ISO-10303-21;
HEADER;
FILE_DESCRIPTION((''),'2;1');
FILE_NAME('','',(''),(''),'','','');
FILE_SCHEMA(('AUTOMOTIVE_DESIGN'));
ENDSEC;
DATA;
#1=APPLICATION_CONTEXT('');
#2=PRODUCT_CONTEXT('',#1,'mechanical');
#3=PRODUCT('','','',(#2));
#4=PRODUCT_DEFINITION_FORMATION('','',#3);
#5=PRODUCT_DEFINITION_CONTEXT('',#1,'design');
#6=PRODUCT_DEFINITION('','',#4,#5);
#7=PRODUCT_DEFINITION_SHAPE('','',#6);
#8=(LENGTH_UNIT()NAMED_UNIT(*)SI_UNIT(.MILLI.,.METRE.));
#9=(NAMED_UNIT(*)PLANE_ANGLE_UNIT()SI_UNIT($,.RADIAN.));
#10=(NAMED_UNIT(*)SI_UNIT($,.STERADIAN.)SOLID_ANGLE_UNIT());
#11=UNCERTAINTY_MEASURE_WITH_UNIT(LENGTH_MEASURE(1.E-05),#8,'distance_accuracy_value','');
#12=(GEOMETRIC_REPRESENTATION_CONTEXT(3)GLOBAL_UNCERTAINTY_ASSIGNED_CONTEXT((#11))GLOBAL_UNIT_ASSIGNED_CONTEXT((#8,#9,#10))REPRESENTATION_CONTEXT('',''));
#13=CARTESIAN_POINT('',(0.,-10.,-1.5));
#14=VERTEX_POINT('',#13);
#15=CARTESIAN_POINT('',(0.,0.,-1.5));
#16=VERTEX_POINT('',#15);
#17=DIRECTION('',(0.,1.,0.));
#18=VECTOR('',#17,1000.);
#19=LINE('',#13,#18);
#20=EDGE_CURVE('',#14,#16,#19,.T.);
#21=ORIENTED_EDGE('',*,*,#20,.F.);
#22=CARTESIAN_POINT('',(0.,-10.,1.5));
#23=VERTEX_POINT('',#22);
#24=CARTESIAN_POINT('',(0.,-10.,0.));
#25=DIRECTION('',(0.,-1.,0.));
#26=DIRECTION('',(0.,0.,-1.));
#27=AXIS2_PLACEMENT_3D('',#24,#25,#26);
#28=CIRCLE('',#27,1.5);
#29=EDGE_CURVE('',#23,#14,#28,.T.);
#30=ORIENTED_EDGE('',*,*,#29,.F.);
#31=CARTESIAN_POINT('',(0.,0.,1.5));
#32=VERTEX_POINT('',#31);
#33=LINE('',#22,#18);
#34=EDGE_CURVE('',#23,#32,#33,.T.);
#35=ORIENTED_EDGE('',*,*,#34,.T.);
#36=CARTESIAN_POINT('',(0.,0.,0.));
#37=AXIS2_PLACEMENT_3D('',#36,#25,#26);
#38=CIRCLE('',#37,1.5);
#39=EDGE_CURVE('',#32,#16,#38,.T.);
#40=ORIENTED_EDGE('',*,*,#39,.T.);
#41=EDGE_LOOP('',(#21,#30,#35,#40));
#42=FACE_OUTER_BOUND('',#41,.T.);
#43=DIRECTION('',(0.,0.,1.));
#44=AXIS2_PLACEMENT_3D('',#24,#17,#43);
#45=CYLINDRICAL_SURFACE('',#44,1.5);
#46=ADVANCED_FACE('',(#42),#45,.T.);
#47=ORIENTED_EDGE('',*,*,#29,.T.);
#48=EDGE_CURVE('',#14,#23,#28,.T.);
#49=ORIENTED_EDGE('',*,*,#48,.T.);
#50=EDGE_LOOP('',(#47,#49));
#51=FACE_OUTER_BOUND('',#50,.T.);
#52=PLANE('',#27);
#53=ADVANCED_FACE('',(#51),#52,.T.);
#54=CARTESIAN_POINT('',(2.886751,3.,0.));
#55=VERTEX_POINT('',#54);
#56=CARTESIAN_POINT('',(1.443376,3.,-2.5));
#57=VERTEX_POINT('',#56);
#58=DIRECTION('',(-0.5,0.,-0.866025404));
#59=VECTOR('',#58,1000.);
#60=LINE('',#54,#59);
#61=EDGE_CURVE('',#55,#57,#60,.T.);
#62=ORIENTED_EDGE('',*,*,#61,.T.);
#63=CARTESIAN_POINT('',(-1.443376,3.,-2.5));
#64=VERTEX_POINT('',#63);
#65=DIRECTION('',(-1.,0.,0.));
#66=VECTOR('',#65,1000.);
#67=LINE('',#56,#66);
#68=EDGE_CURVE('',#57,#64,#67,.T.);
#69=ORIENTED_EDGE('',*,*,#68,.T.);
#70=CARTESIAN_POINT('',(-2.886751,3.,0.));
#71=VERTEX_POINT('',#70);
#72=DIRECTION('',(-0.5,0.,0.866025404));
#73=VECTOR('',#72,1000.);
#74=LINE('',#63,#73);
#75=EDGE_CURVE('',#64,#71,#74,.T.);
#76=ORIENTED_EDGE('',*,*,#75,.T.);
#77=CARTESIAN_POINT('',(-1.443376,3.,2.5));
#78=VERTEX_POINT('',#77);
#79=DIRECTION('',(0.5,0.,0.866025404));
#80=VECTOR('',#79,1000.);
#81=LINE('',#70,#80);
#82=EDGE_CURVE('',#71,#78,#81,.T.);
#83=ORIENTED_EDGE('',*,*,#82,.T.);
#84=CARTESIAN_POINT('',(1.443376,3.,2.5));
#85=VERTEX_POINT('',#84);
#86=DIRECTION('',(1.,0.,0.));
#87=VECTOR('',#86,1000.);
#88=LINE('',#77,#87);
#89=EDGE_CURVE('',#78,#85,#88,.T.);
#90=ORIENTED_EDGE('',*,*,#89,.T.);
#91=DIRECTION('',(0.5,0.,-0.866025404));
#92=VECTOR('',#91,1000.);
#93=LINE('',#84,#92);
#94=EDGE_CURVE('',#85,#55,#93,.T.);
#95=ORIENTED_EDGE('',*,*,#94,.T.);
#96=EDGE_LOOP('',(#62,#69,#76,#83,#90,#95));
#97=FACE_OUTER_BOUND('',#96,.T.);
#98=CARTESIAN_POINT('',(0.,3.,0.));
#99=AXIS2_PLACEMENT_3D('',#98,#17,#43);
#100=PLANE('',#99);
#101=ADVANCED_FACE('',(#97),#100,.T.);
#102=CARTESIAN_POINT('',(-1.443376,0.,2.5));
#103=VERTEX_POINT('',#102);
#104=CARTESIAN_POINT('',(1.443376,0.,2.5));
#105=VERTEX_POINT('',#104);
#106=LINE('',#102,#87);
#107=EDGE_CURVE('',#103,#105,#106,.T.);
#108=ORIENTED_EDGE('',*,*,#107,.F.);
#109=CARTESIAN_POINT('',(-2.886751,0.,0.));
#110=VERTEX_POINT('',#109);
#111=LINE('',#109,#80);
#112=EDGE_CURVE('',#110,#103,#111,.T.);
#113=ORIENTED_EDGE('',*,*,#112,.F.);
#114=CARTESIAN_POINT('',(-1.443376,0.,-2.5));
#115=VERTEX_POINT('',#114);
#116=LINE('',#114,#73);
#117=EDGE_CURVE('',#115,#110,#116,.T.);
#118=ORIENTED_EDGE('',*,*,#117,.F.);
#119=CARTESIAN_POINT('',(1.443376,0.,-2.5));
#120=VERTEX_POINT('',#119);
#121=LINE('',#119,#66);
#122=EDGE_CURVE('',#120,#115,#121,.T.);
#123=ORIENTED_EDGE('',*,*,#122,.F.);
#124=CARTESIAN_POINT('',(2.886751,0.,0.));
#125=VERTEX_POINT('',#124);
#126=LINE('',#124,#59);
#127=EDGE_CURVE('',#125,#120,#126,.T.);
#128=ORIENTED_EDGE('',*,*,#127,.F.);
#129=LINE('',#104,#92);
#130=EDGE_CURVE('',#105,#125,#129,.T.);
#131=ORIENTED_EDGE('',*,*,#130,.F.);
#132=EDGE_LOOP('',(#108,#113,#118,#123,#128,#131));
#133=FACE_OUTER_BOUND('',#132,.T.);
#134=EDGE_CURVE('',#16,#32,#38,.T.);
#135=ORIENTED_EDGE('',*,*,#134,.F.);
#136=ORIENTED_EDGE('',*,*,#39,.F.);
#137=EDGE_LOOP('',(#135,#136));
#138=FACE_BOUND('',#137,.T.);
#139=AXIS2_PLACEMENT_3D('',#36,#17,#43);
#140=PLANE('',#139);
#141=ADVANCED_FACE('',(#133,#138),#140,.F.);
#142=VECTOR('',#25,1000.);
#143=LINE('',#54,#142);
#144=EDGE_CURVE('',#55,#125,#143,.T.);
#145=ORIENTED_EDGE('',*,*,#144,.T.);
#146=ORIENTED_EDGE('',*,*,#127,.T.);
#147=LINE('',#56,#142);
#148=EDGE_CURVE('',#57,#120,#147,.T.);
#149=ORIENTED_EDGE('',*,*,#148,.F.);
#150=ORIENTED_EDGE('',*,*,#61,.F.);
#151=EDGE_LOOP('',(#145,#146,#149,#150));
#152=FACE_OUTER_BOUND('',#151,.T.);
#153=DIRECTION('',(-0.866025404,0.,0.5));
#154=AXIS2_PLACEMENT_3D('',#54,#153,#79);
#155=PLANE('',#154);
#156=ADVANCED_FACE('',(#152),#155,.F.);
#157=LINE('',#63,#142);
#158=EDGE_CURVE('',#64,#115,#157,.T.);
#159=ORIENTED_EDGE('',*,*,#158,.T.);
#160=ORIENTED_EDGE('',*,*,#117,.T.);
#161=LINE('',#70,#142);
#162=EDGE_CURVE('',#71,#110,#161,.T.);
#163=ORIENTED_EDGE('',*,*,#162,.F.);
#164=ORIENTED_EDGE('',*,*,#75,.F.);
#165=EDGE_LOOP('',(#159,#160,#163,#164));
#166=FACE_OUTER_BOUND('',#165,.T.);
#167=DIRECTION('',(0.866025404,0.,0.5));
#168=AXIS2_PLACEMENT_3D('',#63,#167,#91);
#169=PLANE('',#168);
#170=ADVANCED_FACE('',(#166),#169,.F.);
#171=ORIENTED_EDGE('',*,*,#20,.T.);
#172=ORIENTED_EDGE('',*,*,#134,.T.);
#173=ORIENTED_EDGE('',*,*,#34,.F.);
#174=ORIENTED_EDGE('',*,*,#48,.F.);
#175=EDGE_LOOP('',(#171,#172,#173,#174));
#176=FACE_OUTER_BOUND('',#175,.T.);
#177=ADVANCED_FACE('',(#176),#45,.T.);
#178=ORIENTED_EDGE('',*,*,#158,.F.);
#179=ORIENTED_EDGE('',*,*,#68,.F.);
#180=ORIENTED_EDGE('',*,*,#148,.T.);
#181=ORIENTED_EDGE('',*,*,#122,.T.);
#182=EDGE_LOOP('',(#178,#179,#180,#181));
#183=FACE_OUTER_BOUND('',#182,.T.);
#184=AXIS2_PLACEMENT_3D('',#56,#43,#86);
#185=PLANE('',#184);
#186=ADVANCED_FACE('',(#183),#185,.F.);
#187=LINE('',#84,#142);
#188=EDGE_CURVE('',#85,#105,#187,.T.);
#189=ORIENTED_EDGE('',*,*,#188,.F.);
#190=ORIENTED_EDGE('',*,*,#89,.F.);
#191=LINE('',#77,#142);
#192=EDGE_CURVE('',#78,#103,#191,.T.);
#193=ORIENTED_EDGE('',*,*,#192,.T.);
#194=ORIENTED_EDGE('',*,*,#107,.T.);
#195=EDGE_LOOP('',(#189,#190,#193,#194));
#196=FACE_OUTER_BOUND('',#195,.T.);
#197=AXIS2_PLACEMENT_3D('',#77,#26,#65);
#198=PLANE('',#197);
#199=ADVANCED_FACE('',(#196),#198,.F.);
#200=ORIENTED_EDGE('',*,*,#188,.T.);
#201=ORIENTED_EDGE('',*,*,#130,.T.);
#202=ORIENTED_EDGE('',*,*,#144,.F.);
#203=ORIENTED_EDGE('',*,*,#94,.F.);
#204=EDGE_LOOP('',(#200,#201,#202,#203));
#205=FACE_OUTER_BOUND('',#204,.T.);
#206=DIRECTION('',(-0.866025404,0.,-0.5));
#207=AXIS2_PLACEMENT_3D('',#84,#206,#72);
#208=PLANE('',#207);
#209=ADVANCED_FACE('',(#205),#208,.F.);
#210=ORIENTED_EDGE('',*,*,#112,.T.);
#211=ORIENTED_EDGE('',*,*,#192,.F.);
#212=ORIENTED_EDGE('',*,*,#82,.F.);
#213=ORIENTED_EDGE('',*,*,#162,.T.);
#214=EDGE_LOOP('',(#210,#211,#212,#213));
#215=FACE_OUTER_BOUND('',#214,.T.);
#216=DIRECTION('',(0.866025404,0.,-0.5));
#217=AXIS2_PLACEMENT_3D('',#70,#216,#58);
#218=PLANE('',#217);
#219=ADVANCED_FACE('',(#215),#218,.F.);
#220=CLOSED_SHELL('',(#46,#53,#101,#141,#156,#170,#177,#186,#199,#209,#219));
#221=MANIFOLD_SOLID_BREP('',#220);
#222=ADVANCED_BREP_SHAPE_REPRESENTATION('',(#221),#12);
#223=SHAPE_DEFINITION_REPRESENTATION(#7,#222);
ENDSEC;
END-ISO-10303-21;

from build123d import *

# Parameters (mm, degrees)
HEX_HEAD_5AF_X_3_DEPTH = 3
SHANK_PROFILE_3_R      = 1.5
SHANK_3_X_10_DEPTH     = 10


with BuildPart() as part:
    # Hex Head Profile → Hex Head 5AF x 3 (new body)
    with BuildSketch(Plane(origin=(0, 0, 0), x_dir=(1, 0, 0), z_dir=(0, 1, 0))):
        Polygon((2.886751346, 0), (1.443375673, 2.5), (-1.443375673, 2.5), (-2.886751346, 0), (-1.443375673, -2.5), (1.443375673, -2.5), align=None)
    extrude(amount=HEX_HEAD_5AF_X_3_DEPTH)

    # Shank Profile Ø3 → Shank Ø3 x 10 (add)
    with BuildSketch(Plane.XZ):
        with Locations(Location((0, 0, 0), (0, 0, 270))):
            Circle(SHANK_PROFILE_3_R)
    extrude(amount=SHANK_3_X_10_DEPTH)


solid = part.part
